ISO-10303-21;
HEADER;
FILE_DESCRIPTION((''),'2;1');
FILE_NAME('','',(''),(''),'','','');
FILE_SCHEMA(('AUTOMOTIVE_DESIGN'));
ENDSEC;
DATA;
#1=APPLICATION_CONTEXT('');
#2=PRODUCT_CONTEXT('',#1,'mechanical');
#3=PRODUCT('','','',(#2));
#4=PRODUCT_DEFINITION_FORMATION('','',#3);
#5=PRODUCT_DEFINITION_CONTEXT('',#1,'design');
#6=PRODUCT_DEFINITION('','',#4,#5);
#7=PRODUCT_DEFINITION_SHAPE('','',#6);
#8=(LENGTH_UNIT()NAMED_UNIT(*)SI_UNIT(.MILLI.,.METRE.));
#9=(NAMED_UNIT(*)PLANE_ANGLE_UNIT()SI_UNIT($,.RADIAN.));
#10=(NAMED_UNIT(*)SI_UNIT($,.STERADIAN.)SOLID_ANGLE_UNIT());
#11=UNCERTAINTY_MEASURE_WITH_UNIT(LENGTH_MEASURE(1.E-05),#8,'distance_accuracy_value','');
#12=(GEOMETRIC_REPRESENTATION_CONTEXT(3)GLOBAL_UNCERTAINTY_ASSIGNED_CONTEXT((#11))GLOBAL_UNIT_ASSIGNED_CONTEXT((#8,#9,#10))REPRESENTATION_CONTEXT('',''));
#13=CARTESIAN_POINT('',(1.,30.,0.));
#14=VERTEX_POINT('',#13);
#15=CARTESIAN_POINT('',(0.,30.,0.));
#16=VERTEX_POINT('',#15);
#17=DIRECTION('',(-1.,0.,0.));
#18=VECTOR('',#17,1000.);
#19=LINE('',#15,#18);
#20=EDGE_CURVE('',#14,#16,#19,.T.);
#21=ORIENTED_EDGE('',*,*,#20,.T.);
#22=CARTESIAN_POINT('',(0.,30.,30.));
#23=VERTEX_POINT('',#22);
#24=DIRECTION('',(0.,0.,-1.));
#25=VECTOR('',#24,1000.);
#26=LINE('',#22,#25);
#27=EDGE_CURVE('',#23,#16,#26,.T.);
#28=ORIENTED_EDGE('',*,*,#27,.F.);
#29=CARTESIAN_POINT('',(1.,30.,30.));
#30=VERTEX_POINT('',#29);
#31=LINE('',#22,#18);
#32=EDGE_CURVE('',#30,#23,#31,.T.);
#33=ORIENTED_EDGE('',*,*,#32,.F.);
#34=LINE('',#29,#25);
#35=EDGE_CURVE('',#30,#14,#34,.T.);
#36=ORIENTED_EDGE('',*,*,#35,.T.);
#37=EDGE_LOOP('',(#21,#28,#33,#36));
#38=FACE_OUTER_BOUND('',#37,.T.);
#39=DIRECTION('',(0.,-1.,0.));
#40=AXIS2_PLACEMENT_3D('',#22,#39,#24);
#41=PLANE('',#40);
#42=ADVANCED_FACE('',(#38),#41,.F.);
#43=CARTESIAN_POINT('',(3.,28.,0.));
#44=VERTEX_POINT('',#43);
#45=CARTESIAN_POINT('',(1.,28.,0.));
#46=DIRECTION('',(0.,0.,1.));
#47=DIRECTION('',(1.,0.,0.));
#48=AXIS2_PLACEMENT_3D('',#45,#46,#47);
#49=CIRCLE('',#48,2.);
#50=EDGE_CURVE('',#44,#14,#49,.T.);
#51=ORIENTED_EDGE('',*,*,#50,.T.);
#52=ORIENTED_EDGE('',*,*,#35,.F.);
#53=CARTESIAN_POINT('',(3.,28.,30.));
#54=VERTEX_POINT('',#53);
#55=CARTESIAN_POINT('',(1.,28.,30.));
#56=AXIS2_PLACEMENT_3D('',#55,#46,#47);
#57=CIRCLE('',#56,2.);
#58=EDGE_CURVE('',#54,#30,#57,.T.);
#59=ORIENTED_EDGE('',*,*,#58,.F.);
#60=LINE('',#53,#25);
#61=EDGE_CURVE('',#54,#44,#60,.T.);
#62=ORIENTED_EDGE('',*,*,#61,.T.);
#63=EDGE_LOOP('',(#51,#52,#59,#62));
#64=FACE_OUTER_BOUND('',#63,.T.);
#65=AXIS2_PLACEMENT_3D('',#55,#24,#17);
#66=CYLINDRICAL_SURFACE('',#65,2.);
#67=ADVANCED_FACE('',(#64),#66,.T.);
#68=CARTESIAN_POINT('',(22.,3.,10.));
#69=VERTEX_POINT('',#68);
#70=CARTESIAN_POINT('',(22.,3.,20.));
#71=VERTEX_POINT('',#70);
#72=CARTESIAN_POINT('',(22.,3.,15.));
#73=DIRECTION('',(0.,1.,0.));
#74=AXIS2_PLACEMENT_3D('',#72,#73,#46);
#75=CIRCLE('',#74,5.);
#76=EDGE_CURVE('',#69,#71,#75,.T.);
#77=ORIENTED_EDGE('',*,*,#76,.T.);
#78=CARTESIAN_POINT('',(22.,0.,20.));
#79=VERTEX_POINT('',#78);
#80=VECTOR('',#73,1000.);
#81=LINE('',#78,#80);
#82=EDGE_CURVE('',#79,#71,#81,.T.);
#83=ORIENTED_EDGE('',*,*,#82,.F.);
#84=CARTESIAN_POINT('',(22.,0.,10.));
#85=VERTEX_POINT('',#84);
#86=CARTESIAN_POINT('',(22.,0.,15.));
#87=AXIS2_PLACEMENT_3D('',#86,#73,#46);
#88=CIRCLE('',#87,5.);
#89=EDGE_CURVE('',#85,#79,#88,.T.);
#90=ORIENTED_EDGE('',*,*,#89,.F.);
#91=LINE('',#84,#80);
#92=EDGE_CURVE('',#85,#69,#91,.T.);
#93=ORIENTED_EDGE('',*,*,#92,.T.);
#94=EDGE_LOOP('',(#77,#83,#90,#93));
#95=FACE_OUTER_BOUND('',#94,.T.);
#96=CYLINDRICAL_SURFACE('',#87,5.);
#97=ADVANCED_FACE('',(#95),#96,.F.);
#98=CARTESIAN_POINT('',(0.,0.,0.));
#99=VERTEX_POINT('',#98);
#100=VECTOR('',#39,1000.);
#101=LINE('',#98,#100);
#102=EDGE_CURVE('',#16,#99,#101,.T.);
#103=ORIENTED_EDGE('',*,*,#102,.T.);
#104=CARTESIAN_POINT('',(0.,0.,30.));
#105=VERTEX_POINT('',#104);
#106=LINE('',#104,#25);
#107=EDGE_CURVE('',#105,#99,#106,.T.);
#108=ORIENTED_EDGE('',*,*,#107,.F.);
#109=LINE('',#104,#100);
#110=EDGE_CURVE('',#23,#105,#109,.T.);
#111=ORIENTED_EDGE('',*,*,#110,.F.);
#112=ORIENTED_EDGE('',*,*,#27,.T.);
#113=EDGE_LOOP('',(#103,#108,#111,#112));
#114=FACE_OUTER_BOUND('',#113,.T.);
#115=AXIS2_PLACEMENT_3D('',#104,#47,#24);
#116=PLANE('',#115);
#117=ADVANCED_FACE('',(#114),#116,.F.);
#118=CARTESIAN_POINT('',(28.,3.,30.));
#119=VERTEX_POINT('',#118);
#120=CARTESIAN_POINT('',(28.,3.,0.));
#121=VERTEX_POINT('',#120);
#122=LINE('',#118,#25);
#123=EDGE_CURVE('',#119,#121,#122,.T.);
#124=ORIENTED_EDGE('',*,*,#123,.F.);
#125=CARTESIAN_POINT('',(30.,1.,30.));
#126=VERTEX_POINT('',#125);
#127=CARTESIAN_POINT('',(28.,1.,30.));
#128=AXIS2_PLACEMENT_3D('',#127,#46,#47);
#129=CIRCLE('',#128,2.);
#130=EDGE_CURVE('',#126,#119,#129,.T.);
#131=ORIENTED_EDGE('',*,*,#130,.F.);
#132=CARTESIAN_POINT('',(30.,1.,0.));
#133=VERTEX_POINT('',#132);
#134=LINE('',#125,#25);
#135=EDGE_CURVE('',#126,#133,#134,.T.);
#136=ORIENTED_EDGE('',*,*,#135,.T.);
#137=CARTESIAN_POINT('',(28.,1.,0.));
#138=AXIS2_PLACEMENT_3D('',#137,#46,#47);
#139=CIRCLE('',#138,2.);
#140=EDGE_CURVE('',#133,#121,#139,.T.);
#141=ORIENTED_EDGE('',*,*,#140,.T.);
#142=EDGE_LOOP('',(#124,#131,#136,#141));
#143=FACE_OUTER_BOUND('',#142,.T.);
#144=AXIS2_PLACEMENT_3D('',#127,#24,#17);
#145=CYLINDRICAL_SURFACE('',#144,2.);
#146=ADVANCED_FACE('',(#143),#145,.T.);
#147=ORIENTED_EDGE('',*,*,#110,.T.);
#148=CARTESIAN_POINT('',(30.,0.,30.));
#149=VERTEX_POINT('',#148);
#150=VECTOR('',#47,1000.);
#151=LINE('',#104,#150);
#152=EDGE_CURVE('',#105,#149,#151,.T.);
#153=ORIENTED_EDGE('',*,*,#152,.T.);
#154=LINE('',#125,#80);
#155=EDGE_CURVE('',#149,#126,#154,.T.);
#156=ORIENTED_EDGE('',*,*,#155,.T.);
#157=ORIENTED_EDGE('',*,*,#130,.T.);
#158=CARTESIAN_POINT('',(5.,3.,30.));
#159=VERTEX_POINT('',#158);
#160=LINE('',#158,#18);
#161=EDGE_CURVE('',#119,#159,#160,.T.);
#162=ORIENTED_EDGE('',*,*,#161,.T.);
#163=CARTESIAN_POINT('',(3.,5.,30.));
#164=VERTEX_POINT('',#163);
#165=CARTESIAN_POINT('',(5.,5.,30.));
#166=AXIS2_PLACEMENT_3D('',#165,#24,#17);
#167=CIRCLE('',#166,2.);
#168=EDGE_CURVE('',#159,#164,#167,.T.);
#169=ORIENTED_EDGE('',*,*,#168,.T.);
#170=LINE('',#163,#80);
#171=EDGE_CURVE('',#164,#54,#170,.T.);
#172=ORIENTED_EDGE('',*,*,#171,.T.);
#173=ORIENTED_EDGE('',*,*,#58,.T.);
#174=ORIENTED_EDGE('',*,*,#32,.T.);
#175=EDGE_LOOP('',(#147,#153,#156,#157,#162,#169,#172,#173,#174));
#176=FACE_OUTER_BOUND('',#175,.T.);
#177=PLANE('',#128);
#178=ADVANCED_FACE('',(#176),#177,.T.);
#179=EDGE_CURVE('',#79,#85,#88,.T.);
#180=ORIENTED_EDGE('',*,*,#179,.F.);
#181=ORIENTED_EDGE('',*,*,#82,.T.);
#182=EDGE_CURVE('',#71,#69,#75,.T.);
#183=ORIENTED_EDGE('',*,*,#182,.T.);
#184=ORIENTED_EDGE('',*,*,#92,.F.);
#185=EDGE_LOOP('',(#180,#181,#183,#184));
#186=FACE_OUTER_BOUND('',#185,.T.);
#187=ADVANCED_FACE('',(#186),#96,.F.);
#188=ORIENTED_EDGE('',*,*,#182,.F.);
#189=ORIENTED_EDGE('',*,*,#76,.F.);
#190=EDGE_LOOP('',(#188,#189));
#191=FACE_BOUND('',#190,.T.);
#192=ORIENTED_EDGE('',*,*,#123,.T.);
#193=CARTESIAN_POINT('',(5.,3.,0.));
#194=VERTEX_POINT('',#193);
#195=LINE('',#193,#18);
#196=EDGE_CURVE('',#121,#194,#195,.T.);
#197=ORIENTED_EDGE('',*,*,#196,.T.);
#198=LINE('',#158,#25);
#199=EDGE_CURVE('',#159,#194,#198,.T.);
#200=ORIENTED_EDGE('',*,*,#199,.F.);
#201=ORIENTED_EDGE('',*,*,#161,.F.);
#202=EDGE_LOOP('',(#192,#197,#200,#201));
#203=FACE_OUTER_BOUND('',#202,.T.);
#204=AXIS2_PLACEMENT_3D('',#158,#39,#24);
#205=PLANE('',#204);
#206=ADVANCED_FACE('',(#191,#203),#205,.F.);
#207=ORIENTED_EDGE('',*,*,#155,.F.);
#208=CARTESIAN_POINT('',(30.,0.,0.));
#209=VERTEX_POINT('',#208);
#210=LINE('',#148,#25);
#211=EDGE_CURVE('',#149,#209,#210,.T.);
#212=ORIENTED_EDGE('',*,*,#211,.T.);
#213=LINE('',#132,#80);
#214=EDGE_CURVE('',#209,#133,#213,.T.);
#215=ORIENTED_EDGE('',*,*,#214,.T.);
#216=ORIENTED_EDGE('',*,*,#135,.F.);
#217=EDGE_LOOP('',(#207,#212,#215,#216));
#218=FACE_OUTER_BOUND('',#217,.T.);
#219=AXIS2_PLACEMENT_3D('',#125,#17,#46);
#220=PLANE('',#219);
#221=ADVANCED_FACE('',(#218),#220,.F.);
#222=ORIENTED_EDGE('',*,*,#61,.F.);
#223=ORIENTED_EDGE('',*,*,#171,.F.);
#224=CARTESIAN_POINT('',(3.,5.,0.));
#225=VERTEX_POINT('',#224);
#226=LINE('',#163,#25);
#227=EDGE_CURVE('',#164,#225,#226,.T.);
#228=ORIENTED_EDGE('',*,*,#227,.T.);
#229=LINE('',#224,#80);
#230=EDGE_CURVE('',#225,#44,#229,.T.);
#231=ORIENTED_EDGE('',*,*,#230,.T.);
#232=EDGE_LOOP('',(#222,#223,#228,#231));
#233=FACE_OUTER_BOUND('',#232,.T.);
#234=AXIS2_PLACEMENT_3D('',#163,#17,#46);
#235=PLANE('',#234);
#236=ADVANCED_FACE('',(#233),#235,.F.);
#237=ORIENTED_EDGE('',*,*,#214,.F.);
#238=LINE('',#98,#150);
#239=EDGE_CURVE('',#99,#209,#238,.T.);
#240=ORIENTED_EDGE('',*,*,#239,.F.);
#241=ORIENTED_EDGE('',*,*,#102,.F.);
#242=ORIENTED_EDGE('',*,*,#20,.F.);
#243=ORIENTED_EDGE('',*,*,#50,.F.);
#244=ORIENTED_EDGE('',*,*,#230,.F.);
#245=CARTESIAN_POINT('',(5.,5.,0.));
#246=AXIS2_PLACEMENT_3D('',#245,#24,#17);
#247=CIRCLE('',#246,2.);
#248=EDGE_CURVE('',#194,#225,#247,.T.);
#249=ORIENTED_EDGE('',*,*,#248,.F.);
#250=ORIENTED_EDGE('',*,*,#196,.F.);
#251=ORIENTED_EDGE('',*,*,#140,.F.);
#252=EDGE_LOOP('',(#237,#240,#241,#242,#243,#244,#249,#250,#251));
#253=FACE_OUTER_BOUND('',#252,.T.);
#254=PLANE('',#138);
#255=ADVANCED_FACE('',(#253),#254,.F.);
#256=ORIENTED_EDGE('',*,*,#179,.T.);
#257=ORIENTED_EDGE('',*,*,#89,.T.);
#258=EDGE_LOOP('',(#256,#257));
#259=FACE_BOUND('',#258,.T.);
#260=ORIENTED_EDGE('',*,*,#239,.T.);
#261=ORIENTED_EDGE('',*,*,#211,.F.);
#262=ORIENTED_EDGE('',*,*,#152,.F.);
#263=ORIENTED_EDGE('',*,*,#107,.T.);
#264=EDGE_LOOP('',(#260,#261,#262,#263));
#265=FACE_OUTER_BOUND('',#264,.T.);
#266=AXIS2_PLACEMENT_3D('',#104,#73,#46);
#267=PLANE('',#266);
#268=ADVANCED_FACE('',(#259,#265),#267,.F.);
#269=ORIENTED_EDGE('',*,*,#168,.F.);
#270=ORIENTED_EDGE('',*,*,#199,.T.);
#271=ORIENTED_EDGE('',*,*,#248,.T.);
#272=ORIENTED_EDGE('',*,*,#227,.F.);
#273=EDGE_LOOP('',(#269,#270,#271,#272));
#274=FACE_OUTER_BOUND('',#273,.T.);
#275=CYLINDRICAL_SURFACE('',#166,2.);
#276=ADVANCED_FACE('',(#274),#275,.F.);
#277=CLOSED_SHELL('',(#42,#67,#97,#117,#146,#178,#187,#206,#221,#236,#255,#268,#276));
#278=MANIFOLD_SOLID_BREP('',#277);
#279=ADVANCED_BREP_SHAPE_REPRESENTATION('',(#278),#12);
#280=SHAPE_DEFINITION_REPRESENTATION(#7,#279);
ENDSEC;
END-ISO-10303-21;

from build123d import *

# Parameters (mm, degrees)
BOSS_EXTRUDE1_DEPTH = 30
SKETCH3_R           = 5
CUT_EXTRUDE1_DEPTH  = 3


with BuildPart() as part:
    # Sketch2 → Boss-Extrude1 (new body)
    with BuildSketch(Plane.XY):
        with BuildLine():
            Line((0, 0), (0, 30))
            Line((0, 30), (1, 30))
            ThreePointArc((1, 30), (2.414213562, 29.414213562), (3, 28))
            Line((3, 28), (3, 5))
            ThreePointArc((3, 5), (3.585786438, 3.585786438), (5, 3))
            Line((5, 3), (28, 3))
            ThreePointArc((28, 3), (29.414213562, 2.414213562), (30, 1))
            Line((30, 1), (30, 0))
            Line((30, 0), (0, 0))
        make_face()
    extrude(amount=BOSS_EXTRUDE1_DEPTH)

    # Sketch3 → Cut-Extrude1 (cut)
    with BuildSketch(Plane(origin=(0, 3, 0), x_dir=(1, 0, 0), z_dir=(0, 1, 0))):
        with Locations(Location((22, -15, 0), (0, 0, 270))):
            Circle(SKETCH3_R)
    extrude(amount=-CUT_EXTRUDE1_DEPTH, mode=Mode.SUBTRACT)


solid = part.part
